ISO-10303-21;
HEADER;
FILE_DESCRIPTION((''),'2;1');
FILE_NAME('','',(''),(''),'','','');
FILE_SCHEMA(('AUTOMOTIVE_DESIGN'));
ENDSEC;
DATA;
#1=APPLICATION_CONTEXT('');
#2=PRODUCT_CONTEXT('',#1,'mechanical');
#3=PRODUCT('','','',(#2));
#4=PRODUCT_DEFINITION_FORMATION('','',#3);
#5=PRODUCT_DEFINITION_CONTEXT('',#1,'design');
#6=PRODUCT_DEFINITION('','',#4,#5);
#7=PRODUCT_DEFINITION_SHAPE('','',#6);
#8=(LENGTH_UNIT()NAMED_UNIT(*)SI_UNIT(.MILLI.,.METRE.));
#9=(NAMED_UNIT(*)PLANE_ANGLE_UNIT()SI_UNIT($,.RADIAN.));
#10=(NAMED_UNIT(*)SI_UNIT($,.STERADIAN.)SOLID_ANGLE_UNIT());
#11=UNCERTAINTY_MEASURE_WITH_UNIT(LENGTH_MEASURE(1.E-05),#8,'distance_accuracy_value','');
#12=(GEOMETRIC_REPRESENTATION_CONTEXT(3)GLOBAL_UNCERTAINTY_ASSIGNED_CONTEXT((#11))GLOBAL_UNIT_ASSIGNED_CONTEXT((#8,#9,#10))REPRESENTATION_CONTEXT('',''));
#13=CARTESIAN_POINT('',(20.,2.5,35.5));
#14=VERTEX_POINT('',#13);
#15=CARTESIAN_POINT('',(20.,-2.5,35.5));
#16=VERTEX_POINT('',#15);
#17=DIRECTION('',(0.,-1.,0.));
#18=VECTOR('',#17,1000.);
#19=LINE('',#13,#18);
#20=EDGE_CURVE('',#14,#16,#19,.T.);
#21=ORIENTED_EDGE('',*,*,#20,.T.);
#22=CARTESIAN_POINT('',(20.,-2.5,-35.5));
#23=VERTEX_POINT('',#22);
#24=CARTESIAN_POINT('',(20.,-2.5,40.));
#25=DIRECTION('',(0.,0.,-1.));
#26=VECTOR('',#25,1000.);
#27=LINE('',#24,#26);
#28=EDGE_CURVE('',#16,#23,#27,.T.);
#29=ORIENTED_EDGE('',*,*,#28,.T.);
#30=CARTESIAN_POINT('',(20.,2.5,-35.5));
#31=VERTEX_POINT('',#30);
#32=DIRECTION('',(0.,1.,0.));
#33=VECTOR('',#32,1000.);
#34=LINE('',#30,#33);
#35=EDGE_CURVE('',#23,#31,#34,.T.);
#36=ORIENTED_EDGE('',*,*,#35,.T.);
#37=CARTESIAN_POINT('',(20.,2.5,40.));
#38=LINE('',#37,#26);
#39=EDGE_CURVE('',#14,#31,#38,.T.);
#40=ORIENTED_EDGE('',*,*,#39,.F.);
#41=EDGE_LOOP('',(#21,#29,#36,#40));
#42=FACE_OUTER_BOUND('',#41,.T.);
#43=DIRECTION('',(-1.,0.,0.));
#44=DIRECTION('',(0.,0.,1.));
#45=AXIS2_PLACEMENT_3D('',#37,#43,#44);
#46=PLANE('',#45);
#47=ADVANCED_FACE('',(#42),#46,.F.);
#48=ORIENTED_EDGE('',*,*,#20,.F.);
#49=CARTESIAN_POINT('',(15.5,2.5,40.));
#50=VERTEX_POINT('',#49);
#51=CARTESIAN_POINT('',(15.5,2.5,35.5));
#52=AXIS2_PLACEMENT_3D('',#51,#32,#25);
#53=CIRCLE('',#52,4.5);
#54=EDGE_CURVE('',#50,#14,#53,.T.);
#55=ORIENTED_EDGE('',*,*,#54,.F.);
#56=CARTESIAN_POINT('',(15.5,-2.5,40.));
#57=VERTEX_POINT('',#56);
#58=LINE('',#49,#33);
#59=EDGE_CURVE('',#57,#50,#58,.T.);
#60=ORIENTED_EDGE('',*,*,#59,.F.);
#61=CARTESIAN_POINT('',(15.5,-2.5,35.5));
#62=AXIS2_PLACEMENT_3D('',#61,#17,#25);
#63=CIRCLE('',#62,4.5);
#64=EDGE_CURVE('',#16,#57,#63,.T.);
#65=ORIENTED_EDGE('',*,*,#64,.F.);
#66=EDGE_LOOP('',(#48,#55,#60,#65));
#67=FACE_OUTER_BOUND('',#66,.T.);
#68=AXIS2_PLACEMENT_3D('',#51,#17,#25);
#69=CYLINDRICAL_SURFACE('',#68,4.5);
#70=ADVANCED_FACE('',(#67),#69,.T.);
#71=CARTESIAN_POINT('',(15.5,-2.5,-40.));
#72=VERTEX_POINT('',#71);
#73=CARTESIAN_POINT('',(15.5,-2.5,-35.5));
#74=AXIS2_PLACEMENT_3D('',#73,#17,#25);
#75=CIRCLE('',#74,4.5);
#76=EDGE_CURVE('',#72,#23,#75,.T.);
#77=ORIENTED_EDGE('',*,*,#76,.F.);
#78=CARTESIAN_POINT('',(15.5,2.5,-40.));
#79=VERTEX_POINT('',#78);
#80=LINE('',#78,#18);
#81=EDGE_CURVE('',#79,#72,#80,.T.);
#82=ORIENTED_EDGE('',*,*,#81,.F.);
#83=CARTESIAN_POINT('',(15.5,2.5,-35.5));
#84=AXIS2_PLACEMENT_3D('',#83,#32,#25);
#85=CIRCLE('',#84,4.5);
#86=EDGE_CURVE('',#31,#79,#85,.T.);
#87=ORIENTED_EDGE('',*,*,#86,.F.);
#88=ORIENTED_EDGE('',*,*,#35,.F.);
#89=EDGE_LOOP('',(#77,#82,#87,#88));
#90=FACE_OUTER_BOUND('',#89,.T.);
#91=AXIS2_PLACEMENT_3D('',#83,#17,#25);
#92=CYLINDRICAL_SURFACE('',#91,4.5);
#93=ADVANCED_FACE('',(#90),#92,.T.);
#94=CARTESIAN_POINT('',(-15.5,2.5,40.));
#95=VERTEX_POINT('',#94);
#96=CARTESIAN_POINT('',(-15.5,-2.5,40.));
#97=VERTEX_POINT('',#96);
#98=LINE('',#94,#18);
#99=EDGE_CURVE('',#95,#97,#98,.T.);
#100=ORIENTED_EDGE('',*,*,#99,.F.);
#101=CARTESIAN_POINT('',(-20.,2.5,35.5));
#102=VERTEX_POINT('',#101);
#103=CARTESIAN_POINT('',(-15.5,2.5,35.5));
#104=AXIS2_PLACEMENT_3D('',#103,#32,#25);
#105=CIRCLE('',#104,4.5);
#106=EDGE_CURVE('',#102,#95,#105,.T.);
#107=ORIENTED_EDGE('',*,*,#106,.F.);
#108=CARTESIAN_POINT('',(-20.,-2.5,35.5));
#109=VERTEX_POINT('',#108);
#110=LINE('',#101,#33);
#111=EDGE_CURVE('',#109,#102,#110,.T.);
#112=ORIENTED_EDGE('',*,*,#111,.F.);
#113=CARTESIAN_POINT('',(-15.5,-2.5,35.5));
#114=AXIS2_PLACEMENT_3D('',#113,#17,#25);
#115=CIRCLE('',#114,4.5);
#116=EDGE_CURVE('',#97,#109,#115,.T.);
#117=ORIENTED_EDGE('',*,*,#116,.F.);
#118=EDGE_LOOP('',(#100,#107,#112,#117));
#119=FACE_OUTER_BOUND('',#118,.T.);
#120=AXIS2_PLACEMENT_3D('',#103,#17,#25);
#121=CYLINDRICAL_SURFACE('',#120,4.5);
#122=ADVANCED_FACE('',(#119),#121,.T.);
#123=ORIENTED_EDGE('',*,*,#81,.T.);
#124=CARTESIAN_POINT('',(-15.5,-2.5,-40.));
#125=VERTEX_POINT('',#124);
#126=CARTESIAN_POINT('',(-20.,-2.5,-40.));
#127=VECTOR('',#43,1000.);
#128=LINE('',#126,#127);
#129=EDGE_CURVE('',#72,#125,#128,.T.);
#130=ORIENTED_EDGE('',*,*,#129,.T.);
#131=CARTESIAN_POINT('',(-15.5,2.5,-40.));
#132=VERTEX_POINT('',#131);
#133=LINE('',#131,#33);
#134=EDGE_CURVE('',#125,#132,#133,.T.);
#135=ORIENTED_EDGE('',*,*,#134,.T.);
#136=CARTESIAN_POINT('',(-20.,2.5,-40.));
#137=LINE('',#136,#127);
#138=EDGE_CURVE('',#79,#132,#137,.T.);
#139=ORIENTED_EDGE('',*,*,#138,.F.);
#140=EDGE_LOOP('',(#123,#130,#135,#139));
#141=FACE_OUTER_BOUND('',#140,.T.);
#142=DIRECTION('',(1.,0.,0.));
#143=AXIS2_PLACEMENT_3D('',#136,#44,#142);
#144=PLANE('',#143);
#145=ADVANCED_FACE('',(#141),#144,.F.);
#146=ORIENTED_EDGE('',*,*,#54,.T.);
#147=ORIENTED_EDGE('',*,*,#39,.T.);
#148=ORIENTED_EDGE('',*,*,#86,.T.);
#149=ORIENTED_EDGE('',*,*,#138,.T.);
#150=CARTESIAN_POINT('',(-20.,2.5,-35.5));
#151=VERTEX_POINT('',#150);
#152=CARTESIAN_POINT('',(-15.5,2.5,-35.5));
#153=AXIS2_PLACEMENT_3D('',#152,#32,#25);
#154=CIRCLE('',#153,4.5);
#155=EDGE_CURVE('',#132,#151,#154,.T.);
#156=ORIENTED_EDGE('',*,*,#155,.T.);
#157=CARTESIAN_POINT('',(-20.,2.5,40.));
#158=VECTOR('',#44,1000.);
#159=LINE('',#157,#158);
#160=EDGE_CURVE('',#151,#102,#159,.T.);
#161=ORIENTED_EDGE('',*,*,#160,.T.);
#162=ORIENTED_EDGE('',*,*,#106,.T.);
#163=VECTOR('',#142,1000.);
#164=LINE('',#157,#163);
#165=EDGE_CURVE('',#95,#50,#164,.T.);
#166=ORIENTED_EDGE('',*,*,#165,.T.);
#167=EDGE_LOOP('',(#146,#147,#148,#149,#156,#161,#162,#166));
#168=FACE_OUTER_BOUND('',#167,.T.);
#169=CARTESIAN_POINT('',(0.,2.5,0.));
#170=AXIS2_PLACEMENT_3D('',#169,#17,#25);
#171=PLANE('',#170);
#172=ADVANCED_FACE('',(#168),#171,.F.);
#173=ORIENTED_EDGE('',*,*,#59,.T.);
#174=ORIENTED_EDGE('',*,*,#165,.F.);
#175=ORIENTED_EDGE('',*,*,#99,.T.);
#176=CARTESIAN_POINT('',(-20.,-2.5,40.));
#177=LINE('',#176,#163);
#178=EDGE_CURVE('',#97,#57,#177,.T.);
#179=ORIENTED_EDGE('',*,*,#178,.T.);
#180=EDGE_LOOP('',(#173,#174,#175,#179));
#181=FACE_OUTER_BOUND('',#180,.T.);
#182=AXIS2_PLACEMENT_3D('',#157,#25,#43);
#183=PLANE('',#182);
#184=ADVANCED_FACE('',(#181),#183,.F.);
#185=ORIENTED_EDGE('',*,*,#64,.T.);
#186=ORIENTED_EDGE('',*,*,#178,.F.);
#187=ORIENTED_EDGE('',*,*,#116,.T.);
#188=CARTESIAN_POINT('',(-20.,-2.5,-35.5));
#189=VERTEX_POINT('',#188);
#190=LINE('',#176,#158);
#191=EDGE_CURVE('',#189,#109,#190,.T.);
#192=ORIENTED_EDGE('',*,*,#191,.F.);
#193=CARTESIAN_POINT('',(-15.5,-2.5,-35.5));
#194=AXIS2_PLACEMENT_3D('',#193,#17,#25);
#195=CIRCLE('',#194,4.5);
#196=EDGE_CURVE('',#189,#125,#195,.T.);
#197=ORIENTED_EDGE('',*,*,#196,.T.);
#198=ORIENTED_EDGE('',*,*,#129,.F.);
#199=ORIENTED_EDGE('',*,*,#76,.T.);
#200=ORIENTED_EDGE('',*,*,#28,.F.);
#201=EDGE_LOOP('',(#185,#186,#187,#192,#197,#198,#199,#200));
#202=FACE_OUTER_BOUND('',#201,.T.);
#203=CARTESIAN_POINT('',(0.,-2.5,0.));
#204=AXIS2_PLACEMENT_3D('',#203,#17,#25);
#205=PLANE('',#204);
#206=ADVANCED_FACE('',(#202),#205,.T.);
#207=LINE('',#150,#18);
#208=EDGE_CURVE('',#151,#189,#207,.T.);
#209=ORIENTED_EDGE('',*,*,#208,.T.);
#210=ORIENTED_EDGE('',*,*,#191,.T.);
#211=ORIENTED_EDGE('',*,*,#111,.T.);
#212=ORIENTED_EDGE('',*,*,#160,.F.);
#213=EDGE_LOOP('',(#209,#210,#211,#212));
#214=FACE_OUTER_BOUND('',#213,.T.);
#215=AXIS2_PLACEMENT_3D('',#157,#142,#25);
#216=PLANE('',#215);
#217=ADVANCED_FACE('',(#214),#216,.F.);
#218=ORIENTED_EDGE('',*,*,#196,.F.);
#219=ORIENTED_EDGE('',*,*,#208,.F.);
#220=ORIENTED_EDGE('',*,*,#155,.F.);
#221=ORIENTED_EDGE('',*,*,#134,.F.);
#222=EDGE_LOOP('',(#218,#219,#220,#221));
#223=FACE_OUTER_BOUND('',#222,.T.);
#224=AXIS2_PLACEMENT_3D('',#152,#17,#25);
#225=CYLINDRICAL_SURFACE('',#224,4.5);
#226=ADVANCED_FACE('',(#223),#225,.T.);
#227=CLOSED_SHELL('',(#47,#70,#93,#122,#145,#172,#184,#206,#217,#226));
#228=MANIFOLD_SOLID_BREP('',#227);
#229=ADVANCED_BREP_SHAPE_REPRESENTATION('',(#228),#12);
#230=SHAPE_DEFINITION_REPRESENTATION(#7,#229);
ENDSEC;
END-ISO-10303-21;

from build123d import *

# Parameters (mm, degrees)
SKETCH_1_W      = 40
SKETCH_1_H      = 80
EXTRUDE_1_DEPTH = 2.5
FILLET_1_R      = 4.5


with BuildPart() as part:
    # 草图1 → 凸台-拉伸1 (new, symmetric)
    with BuildSketch(Plane(origin=(0, 0, 0), x_dir=(1, 0, 0), z_dir=(0, 1, 0))):
        Rectangle(SKETCH_1_W, SKETCH_1_H)
    extrude(amount=EXTRUDE_1_DEPTH, both=True)

    # 圆角1
    fillet_1_edges = [part.edges().sort_by_distance(p)[0] for p in [
        (20, 0, 40),
        (-20, 0, 40),
        (-20, 0, -40),
        (20, 0, -40),
    ]]
    fillet(fillet_1_edges, radius=FILLET_1_R)


solid = part.part
